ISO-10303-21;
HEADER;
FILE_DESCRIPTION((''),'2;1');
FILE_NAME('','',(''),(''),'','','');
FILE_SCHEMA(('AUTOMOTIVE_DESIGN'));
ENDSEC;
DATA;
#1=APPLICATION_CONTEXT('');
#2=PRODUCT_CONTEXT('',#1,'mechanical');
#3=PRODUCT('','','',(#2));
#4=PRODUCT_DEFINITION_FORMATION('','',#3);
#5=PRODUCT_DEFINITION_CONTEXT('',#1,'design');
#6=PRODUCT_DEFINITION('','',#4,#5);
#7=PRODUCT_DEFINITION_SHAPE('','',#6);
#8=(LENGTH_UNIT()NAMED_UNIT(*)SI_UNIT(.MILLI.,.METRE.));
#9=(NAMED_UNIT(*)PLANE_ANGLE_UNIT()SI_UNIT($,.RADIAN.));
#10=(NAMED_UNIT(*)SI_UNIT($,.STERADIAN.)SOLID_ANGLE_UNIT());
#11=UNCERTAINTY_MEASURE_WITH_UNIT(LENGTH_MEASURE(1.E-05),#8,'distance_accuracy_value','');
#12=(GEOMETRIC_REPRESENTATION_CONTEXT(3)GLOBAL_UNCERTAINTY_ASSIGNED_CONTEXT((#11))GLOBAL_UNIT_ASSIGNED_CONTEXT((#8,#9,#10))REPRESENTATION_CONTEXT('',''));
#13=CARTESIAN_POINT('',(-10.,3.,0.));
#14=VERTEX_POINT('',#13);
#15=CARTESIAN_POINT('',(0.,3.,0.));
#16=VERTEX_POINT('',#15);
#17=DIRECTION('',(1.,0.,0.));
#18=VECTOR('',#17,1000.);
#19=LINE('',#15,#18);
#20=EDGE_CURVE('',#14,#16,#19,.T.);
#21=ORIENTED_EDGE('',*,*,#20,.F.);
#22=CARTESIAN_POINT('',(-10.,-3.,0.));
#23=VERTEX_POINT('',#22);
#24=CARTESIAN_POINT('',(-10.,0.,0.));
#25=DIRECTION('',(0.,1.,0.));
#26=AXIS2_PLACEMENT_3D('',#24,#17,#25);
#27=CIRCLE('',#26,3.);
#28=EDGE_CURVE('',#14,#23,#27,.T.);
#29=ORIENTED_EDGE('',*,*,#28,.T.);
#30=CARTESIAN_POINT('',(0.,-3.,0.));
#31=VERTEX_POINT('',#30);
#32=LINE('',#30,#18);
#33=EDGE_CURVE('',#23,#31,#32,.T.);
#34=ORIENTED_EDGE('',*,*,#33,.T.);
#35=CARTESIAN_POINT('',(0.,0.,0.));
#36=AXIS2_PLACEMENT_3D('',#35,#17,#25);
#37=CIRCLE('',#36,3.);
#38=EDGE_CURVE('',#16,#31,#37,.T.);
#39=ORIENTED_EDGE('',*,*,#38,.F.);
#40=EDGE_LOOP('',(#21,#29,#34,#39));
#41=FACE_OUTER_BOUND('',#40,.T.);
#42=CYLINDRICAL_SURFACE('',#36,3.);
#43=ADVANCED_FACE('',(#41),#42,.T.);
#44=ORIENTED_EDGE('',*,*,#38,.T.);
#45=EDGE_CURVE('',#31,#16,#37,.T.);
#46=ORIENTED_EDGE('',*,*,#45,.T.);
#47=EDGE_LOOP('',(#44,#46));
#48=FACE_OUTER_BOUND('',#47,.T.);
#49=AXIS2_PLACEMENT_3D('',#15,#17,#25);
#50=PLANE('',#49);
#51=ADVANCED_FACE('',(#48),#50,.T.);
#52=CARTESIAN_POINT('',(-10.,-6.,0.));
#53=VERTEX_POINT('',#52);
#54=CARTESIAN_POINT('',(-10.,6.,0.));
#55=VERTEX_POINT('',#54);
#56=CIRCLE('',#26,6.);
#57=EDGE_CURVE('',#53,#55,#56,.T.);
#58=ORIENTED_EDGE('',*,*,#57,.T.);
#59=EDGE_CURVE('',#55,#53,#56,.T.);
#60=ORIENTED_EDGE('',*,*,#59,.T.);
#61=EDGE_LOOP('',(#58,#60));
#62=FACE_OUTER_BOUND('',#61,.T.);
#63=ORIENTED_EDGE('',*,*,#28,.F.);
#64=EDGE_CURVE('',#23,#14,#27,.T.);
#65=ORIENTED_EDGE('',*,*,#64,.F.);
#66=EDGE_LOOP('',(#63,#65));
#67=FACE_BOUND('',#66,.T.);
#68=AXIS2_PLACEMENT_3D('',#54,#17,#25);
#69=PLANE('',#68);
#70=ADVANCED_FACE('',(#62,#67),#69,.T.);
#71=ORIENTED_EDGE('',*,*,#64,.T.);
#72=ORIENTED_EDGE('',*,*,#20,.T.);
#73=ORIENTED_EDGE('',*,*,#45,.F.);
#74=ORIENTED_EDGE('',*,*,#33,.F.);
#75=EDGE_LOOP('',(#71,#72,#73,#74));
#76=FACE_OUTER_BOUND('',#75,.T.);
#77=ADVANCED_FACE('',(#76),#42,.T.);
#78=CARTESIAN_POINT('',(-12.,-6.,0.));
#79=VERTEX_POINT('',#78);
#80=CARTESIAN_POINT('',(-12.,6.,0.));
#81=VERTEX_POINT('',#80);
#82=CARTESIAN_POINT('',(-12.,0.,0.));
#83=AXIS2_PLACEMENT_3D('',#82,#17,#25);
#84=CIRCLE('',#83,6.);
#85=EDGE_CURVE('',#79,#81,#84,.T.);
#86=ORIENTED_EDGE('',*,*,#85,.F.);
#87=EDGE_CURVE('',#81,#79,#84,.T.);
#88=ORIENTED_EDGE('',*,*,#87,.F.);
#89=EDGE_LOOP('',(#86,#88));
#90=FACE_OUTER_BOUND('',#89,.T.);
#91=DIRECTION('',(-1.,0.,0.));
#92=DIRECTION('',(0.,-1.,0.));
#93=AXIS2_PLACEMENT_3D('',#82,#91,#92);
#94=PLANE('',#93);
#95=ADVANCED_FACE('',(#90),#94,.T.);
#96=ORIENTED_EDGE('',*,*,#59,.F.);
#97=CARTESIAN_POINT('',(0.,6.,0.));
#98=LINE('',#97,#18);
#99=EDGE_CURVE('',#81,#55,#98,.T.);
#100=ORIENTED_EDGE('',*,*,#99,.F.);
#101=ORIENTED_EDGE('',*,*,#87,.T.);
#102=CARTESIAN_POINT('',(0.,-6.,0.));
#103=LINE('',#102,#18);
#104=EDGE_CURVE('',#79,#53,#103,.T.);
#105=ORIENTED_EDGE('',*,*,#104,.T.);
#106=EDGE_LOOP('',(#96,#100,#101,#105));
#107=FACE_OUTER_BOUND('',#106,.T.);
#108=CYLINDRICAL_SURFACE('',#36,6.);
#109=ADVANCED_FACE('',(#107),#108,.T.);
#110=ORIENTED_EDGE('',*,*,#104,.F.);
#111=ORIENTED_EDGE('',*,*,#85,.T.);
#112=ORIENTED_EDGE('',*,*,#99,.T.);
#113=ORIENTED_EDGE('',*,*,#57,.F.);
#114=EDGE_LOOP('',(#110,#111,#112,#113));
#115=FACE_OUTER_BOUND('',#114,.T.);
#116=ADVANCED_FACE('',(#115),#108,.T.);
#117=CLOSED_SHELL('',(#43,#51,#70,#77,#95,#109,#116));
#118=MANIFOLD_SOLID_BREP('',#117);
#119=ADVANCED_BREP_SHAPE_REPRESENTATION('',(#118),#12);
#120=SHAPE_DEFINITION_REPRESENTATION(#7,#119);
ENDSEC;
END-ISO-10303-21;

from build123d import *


with BuildPart() as part:
    # Pin Profile Sketch → Headed Pin Revolve (revolve)
    with BuildSketch(Plane.XY):
        Polygon((0, 0), (-12, 0), (-12, 6), (-10, 6), (-10, 3), (0, 3), align=None)
    revolve(axis=Axis((0, 0, 0), (-1, 0, 0)))


solid = part.part
